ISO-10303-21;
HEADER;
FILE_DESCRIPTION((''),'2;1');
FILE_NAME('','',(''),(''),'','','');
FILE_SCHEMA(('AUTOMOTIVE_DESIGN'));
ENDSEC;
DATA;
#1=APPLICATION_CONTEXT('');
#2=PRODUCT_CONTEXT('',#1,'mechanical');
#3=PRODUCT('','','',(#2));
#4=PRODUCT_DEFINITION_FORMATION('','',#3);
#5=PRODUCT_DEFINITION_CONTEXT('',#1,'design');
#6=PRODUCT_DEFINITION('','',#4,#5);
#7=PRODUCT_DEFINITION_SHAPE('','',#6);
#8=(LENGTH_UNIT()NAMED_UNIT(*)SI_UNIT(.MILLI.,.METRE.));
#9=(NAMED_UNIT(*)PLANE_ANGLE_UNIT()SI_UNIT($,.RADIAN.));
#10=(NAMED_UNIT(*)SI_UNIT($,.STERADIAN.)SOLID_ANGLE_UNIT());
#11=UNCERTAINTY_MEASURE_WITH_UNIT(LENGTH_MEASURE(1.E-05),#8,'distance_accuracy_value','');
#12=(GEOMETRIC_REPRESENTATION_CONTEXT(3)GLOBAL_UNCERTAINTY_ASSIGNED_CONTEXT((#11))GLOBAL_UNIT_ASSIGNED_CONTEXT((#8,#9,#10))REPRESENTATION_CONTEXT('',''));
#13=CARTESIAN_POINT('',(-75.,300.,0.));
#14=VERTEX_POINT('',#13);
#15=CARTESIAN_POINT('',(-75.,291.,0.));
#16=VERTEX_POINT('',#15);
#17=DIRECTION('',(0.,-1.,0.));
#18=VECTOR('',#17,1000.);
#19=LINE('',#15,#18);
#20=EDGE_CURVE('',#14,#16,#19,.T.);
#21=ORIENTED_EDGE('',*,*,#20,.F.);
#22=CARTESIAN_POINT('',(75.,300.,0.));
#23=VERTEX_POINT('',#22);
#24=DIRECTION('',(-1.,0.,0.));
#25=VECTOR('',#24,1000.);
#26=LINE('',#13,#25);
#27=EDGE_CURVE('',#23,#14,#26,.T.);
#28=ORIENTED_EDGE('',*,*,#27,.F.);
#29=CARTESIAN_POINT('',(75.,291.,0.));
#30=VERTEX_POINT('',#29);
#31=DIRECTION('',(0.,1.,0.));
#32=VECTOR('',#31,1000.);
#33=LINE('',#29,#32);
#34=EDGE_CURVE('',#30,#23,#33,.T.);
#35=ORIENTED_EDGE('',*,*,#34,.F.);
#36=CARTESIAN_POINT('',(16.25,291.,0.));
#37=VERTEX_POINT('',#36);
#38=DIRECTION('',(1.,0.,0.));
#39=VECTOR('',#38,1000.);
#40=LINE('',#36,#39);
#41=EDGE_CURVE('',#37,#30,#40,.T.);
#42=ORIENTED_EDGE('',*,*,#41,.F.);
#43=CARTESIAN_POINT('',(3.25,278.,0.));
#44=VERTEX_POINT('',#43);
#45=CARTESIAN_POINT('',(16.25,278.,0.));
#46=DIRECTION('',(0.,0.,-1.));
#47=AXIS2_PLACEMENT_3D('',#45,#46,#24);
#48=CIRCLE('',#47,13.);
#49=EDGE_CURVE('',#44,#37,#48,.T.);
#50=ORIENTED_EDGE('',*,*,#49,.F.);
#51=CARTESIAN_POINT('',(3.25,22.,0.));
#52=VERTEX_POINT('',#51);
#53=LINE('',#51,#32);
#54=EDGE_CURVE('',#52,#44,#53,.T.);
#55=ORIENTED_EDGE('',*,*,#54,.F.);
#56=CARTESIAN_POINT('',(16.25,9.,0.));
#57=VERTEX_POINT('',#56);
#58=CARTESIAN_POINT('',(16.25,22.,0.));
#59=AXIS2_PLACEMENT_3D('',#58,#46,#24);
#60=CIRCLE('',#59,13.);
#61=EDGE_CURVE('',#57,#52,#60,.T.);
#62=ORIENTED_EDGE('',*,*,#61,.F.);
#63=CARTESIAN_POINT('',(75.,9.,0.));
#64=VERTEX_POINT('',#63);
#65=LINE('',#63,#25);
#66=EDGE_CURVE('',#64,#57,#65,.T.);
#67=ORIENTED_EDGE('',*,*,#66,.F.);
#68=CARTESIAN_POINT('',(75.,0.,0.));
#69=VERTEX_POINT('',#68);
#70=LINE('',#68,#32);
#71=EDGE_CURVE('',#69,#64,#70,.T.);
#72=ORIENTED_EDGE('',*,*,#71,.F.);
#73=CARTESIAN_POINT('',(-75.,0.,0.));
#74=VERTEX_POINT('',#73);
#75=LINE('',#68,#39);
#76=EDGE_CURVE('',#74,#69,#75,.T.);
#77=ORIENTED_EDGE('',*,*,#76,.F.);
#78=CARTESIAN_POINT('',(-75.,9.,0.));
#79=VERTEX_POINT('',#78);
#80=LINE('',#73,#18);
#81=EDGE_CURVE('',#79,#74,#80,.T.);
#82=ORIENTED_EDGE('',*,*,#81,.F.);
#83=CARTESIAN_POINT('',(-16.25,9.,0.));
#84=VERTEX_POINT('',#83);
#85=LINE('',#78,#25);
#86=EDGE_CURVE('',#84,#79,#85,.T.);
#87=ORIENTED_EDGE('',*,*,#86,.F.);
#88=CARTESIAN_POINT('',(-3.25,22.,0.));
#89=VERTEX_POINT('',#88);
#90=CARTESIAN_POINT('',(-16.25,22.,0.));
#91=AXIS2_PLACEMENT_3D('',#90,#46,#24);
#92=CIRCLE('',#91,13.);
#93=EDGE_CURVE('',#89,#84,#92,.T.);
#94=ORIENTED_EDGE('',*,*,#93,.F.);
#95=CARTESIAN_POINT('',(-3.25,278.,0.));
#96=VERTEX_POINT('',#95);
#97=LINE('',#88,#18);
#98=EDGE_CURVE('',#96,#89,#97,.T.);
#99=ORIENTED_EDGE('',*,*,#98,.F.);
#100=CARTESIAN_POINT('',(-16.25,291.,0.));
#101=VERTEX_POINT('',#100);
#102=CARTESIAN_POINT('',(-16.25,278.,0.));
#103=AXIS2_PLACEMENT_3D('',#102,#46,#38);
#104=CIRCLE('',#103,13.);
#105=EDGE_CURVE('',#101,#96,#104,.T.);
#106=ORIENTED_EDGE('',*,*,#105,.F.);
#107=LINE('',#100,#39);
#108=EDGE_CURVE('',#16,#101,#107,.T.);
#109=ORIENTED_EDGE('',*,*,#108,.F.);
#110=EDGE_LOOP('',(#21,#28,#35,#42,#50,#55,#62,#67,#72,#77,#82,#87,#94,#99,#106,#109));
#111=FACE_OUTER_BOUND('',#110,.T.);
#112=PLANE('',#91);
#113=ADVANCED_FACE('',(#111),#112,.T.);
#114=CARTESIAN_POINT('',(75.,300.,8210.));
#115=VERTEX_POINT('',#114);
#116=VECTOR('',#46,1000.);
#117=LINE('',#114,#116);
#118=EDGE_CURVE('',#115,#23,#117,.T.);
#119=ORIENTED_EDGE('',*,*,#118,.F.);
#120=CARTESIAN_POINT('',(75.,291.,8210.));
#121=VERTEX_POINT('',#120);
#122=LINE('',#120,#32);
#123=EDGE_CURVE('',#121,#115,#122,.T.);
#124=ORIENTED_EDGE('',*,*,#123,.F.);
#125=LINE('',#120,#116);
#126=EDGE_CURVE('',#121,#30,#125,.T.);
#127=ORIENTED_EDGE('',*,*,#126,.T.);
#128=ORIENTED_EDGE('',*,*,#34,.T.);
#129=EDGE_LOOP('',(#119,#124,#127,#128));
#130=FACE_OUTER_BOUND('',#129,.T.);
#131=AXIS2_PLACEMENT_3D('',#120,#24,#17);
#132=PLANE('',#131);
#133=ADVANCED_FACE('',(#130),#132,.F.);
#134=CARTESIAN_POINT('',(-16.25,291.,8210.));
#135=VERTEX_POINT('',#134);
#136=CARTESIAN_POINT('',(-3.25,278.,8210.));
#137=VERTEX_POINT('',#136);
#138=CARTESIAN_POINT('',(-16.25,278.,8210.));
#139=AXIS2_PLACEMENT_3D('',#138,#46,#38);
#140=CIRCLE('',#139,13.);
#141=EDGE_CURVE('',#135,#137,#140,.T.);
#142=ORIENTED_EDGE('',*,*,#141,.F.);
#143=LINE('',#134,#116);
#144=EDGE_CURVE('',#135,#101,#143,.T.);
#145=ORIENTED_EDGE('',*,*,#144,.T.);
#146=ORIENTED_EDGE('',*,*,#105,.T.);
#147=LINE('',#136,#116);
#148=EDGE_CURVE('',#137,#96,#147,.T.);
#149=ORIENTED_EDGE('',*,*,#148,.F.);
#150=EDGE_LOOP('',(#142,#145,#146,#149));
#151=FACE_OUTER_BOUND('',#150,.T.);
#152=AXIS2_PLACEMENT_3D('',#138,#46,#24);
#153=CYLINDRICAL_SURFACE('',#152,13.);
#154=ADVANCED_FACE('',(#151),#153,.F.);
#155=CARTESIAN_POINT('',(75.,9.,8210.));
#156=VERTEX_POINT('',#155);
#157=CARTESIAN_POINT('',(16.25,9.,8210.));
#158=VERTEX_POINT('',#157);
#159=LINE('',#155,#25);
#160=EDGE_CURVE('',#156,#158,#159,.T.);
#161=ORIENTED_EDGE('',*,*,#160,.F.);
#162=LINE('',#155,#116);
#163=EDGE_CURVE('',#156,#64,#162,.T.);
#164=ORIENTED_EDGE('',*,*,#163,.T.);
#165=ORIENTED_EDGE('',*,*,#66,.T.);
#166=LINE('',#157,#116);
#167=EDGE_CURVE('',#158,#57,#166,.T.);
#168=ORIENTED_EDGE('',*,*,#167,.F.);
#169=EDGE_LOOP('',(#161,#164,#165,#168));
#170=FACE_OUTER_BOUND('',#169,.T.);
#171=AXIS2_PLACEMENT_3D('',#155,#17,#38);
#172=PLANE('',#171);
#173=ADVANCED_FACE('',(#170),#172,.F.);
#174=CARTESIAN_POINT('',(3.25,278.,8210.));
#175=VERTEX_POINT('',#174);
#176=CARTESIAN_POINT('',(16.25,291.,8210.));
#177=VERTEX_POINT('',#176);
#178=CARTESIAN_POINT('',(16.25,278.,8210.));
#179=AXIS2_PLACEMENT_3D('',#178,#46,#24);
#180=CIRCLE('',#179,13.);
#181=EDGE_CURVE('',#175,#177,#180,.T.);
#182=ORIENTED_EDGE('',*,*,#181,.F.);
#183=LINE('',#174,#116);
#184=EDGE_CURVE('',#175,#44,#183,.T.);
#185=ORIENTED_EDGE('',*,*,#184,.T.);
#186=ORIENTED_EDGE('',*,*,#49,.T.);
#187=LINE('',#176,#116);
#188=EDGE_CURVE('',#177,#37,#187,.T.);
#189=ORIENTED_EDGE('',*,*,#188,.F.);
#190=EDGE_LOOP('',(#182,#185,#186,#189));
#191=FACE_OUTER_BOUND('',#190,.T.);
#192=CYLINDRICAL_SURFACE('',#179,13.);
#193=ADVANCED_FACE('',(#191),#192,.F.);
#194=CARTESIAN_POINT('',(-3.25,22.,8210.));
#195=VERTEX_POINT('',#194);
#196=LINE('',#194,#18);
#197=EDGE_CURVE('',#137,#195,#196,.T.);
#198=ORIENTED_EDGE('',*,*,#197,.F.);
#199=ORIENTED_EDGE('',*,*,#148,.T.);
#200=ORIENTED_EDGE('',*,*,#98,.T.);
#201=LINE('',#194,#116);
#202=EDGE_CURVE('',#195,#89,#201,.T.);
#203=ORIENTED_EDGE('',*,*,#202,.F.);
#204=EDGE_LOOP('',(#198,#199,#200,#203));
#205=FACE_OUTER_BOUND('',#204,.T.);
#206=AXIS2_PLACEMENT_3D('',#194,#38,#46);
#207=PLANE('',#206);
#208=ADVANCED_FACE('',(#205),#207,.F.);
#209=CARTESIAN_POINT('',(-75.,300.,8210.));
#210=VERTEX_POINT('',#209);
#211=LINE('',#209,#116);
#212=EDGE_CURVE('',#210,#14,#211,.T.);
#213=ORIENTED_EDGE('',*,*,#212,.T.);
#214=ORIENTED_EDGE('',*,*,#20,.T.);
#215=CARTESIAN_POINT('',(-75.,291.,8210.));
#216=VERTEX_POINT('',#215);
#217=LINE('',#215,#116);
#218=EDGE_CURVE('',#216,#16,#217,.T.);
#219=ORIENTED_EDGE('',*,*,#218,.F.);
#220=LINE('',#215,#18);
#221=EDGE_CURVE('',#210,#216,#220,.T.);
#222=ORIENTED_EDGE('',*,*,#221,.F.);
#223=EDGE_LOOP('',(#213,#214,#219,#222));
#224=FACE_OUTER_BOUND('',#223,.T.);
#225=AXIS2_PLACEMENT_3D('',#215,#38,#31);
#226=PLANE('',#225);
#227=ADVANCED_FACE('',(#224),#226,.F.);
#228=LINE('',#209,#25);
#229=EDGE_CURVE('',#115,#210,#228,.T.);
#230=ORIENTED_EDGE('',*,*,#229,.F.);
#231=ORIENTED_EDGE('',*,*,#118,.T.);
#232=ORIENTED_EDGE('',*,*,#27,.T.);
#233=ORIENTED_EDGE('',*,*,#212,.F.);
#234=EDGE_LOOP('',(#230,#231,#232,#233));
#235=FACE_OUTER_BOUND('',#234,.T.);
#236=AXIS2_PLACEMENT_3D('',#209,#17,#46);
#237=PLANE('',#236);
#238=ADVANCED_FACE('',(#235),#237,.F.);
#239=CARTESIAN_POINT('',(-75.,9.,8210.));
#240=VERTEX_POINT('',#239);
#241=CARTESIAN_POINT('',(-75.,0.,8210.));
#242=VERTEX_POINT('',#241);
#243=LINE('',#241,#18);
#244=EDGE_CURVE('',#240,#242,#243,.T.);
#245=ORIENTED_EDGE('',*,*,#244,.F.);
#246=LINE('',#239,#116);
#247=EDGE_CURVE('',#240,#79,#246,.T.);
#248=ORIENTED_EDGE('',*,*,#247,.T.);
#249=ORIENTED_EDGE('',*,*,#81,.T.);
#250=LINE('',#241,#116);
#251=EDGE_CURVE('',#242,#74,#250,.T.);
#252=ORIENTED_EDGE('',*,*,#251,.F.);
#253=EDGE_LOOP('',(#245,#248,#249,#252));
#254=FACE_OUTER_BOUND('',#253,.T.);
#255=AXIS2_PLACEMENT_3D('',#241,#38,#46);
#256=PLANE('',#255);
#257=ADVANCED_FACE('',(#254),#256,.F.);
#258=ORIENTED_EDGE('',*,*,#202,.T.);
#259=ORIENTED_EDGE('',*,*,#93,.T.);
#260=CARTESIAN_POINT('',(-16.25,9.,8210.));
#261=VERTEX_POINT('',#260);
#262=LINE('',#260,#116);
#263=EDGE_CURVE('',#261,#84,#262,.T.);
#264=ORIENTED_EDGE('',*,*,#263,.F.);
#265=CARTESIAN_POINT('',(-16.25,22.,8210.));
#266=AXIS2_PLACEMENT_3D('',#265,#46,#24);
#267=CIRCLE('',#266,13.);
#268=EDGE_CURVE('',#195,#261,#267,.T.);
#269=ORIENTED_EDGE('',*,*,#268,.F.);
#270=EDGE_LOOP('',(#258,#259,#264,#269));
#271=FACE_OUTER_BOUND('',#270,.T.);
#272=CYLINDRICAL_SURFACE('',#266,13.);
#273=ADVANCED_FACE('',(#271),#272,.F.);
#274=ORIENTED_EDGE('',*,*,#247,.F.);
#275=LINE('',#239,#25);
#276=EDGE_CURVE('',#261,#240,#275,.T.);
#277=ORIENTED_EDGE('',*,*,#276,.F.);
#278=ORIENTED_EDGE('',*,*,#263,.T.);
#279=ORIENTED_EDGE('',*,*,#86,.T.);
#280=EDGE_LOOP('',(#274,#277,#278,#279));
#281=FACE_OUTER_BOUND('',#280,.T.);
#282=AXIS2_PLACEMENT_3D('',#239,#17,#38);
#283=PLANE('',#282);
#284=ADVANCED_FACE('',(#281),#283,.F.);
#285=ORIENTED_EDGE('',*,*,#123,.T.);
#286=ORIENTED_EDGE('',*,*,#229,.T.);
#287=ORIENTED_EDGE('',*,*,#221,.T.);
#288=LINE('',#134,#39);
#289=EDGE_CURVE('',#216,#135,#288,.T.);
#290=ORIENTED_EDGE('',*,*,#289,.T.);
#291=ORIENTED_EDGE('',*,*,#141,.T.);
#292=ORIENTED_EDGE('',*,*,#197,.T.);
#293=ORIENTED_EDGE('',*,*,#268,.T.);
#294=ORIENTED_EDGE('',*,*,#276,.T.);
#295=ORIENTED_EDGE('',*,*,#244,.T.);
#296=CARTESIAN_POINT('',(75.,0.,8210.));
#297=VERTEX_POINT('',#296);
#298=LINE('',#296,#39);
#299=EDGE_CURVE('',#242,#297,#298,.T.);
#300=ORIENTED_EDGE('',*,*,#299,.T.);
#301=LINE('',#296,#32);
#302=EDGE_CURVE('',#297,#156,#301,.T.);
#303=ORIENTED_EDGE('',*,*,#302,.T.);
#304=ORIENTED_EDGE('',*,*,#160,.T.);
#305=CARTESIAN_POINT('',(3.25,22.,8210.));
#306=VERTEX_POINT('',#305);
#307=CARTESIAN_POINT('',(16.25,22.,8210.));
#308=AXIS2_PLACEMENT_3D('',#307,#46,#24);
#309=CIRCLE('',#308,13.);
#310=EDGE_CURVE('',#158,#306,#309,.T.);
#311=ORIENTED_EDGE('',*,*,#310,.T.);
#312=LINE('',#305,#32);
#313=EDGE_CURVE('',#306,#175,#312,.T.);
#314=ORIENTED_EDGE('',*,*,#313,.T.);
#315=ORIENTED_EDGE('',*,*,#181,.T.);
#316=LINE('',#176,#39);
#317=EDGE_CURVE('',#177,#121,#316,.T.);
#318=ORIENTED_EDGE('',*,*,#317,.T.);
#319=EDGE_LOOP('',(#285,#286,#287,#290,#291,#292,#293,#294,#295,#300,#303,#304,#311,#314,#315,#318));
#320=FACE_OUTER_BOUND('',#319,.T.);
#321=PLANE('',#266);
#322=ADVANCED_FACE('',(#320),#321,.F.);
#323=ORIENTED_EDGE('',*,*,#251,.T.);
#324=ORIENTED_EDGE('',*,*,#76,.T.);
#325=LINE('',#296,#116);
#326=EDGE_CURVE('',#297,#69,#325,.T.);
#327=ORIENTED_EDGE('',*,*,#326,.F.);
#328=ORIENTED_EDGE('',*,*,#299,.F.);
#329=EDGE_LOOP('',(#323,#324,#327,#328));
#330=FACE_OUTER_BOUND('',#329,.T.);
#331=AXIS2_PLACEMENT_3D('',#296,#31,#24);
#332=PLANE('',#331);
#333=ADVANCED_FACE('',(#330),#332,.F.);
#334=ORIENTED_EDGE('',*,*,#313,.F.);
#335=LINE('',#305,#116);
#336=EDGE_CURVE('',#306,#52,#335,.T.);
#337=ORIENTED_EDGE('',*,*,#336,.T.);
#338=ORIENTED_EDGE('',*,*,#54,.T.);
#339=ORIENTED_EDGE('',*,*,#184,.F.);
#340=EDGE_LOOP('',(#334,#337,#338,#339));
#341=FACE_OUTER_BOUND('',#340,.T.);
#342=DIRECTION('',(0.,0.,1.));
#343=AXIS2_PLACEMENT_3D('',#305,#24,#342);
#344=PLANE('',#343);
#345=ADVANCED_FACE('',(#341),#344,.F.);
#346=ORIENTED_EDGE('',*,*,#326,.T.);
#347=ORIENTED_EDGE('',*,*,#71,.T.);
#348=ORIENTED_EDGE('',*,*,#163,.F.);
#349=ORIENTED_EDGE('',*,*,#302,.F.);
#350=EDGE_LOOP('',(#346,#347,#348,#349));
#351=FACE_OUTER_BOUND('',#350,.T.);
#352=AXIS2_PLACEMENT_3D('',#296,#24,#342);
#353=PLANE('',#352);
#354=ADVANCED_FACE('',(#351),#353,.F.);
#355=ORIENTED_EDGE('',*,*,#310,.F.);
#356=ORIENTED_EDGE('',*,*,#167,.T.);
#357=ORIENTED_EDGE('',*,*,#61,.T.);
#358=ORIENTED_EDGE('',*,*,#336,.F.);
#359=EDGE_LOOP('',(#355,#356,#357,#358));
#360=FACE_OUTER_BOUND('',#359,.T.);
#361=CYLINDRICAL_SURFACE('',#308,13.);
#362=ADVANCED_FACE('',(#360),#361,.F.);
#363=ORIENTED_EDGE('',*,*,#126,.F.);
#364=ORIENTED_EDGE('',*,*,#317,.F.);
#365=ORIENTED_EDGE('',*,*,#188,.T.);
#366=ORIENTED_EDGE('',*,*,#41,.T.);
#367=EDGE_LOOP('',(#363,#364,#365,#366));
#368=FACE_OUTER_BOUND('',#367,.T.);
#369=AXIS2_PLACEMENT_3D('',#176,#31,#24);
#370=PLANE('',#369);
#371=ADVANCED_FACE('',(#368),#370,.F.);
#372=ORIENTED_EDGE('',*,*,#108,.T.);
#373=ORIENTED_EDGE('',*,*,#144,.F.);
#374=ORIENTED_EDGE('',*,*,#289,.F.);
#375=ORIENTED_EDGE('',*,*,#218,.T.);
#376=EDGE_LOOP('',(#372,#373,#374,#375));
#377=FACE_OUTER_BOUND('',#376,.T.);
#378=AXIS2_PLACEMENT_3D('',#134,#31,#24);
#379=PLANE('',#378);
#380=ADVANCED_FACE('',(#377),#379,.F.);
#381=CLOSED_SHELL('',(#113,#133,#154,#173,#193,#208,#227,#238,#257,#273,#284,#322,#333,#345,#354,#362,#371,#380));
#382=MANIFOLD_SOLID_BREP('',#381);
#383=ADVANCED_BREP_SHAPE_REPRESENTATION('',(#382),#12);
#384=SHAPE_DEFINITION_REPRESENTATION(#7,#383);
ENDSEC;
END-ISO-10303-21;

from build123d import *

# Parameters (mm, degrees)
BOSS_EXTRUDE1_DEPTH = 8210


with BuildPart() as part:
    # Sketch1 → Boss-Extrude1 (new body)
    with BuildSketch(Plane.XY):
        with BuildLine():
            Line((75, 0), (-75, 0))
            Line((-75, 0), (-75, 9))
            Line((-75, 9), (-16.25, 9))
            ThreePointArc((-16.25, 9), (-7.057611845, 12.807611845), (-3.25, 22))
            Line((-3.25, 22), (-3.25, 278))
            ThreePointArc((-3.25, 278), (-7.057611845, 287.192388155), (-16.25, 291))
            Line((-16.25, 291), (-75, 291))
            Line((-75, 291), (-75, 300))
            Line((-75, 300), (75, 300))
            Line((75, 300), (75, 291))
            Line((75, 291), (16.25, 291))
            ThreePointArc((16.25, 291), (7.057611845, 287.192388155), (3.25, 278))
            Line((3.25, 278), (3.25, 22))
            ThreePointArc((3.25, 22), (7.057611845, 12.807611845), (16.25, 9))
            Line((16.25, 9), (75, 9))
            Line((75, 9), (75, 0))
        make_face()
    extrude(amount=BOSS_EXTRUDE1_DEPTH)


solid = part.part
